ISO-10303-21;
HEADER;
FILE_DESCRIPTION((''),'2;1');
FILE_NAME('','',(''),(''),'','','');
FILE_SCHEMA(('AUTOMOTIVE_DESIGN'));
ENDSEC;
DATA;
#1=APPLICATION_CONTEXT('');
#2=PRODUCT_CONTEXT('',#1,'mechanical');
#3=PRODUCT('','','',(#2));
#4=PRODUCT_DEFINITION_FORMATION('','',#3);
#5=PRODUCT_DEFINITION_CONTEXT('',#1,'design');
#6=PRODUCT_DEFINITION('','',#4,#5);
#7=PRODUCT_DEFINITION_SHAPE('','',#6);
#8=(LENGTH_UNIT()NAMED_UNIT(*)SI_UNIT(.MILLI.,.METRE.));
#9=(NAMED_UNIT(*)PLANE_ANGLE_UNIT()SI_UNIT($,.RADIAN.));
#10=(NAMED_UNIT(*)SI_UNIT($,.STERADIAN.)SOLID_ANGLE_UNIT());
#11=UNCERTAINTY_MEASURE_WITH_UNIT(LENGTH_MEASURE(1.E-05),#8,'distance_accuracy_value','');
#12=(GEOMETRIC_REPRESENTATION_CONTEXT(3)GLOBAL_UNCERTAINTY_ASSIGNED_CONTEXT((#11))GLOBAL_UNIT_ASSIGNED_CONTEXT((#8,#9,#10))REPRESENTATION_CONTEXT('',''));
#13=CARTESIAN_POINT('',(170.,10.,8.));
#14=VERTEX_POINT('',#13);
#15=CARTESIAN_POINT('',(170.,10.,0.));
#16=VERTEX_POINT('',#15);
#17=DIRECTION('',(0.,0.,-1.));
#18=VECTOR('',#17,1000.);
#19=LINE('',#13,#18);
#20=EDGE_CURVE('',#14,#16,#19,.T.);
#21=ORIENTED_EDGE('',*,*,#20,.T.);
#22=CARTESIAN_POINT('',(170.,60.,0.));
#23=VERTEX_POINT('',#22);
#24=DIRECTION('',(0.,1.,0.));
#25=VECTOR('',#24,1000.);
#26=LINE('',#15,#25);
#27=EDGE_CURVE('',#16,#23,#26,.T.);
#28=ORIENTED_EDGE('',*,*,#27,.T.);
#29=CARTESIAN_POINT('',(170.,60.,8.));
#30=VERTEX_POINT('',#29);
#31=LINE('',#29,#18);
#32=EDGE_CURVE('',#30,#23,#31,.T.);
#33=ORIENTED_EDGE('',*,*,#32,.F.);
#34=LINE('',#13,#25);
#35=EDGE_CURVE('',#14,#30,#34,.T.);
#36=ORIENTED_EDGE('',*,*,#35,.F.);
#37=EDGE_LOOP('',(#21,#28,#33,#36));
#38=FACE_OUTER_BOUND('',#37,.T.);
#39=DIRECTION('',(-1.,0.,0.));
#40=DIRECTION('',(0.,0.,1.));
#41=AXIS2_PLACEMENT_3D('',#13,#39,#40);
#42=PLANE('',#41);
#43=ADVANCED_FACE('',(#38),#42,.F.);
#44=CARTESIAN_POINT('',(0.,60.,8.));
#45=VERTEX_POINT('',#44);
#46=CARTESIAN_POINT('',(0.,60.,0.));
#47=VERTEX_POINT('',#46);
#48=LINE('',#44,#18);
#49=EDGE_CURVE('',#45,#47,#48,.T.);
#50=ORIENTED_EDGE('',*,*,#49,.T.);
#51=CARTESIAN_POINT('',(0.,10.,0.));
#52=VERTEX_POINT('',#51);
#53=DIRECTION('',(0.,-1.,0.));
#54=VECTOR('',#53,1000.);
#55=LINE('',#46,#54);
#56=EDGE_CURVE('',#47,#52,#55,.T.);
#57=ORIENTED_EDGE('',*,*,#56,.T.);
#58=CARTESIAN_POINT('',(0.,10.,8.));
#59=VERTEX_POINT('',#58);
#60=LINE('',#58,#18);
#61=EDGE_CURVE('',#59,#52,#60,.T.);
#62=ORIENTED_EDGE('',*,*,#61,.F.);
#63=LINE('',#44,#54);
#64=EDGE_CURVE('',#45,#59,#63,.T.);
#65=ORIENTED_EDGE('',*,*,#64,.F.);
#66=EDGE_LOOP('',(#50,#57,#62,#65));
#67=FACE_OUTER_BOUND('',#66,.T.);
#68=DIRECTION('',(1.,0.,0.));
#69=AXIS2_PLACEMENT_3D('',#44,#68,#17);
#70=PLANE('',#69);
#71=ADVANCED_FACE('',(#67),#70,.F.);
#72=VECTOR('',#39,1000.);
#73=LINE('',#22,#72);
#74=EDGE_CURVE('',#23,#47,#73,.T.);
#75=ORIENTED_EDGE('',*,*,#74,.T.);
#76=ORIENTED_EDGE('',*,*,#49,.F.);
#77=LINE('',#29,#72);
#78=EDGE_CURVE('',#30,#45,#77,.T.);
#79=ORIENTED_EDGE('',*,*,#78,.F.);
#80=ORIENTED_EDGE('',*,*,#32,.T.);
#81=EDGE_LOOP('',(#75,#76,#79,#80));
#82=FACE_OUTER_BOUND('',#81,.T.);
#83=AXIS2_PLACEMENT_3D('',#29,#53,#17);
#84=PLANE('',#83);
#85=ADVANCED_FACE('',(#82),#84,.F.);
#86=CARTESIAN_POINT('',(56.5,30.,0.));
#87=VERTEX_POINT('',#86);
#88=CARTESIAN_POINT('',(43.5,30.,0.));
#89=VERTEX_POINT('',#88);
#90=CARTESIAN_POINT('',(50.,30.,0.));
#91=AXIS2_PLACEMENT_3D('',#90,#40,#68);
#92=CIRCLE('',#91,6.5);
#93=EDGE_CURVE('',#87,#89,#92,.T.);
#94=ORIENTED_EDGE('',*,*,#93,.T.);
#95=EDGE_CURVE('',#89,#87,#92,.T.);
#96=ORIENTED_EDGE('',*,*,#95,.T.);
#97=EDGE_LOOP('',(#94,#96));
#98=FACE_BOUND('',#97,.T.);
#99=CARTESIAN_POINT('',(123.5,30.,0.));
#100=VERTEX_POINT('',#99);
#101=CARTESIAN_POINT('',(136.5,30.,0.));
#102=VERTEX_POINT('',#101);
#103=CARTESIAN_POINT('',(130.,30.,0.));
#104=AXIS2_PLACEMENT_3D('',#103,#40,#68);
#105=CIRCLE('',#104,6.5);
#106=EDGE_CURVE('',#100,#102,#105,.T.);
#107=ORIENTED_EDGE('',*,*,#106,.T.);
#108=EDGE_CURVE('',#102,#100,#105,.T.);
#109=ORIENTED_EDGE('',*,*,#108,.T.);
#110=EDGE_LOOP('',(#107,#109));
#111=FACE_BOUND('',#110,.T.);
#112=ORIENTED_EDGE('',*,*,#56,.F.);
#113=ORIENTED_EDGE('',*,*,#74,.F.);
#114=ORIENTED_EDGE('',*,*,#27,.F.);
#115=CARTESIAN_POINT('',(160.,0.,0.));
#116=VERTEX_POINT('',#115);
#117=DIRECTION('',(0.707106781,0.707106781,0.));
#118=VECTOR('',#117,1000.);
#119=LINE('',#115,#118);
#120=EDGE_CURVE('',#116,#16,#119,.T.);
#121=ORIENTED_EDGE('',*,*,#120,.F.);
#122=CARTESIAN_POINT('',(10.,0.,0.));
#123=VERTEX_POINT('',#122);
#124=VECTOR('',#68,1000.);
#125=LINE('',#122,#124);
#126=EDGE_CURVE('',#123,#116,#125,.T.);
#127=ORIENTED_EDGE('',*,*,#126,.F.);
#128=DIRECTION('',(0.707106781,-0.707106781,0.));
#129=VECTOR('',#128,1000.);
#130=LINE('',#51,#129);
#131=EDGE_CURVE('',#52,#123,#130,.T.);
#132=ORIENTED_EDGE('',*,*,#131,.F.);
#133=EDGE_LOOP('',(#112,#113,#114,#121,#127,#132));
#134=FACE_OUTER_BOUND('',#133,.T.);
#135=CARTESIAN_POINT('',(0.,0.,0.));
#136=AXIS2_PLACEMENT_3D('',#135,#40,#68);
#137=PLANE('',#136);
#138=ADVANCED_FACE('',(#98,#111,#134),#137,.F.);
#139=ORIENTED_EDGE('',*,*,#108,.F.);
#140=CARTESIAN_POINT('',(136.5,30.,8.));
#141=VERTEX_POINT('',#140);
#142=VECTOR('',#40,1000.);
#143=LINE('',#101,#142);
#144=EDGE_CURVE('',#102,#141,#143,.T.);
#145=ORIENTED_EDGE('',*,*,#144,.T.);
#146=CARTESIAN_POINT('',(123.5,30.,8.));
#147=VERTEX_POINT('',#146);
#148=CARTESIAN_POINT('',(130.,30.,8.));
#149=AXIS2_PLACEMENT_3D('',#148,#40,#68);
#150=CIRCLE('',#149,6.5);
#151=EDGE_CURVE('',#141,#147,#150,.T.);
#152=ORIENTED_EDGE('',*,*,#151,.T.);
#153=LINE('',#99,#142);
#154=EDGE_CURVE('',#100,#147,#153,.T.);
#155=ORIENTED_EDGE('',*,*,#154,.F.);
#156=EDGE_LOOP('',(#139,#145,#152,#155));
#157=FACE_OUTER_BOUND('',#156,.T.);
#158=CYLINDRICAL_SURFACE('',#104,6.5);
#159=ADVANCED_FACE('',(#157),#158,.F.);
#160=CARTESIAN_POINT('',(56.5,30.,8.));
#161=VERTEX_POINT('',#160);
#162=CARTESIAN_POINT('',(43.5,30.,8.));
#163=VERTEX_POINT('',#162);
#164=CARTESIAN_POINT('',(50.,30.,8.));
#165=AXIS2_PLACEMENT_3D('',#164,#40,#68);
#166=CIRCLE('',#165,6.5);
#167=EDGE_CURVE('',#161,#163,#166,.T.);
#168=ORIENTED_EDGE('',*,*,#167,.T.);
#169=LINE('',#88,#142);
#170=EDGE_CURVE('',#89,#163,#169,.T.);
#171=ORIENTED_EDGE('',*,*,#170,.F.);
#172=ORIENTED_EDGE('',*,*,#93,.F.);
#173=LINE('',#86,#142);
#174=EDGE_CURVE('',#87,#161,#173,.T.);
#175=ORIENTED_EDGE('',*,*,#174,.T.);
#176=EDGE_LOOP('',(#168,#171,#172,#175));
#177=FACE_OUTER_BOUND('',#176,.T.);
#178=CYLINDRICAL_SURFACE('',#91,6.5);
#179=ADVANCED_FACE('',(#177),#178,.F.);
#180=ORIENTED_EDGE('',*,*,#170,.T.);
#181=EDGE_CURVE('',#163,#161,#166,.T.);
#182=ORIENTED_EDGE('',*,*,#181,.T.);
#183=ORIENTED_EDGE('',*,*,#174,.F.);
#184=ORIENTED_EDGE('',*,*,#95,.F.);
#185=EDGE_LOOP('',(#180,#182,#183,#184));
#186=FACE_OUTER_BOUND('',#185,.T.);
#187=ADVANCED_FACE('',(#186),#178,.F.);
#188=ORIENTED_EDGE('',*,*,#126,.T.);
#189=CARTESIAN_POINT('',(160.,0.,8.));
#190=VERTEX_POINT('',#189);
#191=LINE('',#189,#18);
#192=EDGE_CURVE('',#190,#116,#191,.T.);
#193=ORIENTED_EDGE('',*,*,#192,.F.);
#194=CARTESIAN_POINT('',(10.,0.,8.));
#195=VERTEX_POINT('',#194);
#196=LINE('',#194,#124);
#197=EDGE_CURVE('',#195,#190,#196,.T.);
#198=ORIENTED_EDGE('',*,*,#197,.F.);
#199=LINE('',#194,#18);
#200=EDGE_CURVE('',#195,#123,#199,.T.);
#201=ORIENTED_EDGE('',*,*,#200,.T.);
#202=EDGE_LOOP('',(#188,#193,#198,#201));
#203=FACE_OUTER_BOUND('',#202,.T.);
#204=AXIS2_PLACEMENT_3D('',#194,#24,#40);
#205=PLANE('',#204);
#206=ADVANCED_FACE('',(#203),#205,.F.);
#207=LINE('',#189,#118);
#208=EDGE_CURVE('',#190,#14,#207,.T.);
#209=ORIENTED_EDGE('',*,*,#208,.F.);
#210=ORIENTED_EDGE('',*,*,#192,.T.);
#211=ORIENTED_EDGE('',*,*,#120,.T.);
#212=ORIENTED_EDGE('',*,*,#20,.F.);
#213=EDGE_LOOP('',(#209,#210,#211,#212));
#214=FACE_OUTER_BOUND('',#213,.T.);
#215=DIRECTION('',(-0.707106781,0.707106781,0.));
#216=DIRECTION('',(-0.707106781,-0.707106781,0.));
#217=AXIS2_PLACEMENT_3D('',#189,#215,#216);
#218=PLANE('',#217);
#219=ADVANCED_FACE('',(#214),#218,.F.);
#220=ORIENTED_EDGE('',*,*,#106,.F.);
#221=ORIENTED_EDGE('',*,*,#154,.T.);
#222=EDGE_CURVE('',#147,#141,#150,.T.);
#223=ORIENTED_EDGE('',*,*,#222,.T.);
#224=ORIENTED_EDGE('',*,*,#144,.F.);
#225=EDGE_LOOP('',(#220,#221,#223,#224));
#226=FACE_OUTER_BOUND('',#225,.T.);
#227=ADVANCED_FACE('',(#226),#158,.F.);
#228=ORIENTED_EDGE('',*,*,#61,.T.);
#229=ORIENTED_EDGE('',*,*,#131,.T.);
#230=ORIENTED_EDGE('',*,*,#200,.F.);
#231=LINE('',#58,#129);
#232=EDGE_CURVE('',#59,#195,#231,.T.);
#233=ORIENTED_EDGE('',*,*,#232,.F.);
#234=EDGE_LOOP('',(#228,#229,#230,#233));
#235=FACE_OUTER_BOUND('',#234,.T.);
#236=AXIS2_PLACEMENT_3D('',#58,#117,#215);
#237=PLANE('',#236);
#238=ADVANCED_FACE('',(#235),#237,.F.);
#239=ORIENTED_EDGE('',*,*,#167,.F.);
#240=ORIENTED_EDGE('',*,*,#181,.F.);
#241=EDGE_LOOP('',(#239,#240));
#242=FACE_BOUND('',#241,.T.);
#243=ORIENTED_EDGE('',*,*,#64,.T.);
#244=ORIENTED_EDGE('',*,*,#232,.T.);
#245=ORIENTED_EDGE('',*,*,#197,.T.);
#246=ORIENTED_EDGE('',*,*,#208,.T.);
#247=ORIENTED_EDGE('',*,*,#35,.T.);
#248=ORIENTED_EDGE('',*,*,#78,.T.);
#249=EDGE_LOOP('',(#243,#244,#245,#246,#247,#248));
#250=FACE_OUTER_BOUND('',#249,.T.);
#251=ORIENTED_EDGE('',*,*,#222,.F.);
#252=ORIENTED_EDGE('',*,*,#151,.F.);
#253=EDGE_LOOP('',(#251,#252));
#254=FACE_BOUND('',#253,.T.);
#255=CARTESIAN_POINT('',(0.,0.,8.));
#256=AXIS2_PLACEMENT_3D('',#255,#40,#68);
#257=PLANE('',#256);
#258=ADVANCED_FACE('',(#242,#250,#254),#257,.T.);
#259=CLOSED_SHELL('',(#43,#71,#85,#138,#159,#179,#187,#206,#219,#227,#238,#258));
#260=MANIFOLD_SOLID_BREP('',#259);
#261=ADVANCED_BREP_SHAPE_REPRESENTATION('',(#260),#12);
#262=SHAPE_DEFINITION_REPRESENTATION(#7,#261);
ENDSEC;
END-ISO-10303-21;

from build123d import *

# Parameters (mm, degrees)
EXTRUDE_1_DEPTH     = 8
SKETCH_2_R          = 6.5
CUT_EXTRUDE_1_DEPTH = 8


with BuildPart() as part:
    # 草图1 → 凸台-拉伸1 (new body)
    with BuildSketch(Plane.XY):
        Polygon((10, 0), (160, 0), (170, 10), (170, 60), (0, 60), (0, 10), align=None)
    extrude(amount=EXTRUDE_1_DEPTH)

    # 草图2 → 切除-拉伸1 (cut)
    with BuildSketch(Plane.XY.offset(8)):
        with Locations((50, 30)):
            Circle(SKETCH_2_R)
        with Locations((130, 30)):
            Circle(SKETCH_2_R)
    extrude(amount=-CUT_EXTRUDE_1_DEPTH, mode=Mode.SUBTRACT)


solid = part.part
